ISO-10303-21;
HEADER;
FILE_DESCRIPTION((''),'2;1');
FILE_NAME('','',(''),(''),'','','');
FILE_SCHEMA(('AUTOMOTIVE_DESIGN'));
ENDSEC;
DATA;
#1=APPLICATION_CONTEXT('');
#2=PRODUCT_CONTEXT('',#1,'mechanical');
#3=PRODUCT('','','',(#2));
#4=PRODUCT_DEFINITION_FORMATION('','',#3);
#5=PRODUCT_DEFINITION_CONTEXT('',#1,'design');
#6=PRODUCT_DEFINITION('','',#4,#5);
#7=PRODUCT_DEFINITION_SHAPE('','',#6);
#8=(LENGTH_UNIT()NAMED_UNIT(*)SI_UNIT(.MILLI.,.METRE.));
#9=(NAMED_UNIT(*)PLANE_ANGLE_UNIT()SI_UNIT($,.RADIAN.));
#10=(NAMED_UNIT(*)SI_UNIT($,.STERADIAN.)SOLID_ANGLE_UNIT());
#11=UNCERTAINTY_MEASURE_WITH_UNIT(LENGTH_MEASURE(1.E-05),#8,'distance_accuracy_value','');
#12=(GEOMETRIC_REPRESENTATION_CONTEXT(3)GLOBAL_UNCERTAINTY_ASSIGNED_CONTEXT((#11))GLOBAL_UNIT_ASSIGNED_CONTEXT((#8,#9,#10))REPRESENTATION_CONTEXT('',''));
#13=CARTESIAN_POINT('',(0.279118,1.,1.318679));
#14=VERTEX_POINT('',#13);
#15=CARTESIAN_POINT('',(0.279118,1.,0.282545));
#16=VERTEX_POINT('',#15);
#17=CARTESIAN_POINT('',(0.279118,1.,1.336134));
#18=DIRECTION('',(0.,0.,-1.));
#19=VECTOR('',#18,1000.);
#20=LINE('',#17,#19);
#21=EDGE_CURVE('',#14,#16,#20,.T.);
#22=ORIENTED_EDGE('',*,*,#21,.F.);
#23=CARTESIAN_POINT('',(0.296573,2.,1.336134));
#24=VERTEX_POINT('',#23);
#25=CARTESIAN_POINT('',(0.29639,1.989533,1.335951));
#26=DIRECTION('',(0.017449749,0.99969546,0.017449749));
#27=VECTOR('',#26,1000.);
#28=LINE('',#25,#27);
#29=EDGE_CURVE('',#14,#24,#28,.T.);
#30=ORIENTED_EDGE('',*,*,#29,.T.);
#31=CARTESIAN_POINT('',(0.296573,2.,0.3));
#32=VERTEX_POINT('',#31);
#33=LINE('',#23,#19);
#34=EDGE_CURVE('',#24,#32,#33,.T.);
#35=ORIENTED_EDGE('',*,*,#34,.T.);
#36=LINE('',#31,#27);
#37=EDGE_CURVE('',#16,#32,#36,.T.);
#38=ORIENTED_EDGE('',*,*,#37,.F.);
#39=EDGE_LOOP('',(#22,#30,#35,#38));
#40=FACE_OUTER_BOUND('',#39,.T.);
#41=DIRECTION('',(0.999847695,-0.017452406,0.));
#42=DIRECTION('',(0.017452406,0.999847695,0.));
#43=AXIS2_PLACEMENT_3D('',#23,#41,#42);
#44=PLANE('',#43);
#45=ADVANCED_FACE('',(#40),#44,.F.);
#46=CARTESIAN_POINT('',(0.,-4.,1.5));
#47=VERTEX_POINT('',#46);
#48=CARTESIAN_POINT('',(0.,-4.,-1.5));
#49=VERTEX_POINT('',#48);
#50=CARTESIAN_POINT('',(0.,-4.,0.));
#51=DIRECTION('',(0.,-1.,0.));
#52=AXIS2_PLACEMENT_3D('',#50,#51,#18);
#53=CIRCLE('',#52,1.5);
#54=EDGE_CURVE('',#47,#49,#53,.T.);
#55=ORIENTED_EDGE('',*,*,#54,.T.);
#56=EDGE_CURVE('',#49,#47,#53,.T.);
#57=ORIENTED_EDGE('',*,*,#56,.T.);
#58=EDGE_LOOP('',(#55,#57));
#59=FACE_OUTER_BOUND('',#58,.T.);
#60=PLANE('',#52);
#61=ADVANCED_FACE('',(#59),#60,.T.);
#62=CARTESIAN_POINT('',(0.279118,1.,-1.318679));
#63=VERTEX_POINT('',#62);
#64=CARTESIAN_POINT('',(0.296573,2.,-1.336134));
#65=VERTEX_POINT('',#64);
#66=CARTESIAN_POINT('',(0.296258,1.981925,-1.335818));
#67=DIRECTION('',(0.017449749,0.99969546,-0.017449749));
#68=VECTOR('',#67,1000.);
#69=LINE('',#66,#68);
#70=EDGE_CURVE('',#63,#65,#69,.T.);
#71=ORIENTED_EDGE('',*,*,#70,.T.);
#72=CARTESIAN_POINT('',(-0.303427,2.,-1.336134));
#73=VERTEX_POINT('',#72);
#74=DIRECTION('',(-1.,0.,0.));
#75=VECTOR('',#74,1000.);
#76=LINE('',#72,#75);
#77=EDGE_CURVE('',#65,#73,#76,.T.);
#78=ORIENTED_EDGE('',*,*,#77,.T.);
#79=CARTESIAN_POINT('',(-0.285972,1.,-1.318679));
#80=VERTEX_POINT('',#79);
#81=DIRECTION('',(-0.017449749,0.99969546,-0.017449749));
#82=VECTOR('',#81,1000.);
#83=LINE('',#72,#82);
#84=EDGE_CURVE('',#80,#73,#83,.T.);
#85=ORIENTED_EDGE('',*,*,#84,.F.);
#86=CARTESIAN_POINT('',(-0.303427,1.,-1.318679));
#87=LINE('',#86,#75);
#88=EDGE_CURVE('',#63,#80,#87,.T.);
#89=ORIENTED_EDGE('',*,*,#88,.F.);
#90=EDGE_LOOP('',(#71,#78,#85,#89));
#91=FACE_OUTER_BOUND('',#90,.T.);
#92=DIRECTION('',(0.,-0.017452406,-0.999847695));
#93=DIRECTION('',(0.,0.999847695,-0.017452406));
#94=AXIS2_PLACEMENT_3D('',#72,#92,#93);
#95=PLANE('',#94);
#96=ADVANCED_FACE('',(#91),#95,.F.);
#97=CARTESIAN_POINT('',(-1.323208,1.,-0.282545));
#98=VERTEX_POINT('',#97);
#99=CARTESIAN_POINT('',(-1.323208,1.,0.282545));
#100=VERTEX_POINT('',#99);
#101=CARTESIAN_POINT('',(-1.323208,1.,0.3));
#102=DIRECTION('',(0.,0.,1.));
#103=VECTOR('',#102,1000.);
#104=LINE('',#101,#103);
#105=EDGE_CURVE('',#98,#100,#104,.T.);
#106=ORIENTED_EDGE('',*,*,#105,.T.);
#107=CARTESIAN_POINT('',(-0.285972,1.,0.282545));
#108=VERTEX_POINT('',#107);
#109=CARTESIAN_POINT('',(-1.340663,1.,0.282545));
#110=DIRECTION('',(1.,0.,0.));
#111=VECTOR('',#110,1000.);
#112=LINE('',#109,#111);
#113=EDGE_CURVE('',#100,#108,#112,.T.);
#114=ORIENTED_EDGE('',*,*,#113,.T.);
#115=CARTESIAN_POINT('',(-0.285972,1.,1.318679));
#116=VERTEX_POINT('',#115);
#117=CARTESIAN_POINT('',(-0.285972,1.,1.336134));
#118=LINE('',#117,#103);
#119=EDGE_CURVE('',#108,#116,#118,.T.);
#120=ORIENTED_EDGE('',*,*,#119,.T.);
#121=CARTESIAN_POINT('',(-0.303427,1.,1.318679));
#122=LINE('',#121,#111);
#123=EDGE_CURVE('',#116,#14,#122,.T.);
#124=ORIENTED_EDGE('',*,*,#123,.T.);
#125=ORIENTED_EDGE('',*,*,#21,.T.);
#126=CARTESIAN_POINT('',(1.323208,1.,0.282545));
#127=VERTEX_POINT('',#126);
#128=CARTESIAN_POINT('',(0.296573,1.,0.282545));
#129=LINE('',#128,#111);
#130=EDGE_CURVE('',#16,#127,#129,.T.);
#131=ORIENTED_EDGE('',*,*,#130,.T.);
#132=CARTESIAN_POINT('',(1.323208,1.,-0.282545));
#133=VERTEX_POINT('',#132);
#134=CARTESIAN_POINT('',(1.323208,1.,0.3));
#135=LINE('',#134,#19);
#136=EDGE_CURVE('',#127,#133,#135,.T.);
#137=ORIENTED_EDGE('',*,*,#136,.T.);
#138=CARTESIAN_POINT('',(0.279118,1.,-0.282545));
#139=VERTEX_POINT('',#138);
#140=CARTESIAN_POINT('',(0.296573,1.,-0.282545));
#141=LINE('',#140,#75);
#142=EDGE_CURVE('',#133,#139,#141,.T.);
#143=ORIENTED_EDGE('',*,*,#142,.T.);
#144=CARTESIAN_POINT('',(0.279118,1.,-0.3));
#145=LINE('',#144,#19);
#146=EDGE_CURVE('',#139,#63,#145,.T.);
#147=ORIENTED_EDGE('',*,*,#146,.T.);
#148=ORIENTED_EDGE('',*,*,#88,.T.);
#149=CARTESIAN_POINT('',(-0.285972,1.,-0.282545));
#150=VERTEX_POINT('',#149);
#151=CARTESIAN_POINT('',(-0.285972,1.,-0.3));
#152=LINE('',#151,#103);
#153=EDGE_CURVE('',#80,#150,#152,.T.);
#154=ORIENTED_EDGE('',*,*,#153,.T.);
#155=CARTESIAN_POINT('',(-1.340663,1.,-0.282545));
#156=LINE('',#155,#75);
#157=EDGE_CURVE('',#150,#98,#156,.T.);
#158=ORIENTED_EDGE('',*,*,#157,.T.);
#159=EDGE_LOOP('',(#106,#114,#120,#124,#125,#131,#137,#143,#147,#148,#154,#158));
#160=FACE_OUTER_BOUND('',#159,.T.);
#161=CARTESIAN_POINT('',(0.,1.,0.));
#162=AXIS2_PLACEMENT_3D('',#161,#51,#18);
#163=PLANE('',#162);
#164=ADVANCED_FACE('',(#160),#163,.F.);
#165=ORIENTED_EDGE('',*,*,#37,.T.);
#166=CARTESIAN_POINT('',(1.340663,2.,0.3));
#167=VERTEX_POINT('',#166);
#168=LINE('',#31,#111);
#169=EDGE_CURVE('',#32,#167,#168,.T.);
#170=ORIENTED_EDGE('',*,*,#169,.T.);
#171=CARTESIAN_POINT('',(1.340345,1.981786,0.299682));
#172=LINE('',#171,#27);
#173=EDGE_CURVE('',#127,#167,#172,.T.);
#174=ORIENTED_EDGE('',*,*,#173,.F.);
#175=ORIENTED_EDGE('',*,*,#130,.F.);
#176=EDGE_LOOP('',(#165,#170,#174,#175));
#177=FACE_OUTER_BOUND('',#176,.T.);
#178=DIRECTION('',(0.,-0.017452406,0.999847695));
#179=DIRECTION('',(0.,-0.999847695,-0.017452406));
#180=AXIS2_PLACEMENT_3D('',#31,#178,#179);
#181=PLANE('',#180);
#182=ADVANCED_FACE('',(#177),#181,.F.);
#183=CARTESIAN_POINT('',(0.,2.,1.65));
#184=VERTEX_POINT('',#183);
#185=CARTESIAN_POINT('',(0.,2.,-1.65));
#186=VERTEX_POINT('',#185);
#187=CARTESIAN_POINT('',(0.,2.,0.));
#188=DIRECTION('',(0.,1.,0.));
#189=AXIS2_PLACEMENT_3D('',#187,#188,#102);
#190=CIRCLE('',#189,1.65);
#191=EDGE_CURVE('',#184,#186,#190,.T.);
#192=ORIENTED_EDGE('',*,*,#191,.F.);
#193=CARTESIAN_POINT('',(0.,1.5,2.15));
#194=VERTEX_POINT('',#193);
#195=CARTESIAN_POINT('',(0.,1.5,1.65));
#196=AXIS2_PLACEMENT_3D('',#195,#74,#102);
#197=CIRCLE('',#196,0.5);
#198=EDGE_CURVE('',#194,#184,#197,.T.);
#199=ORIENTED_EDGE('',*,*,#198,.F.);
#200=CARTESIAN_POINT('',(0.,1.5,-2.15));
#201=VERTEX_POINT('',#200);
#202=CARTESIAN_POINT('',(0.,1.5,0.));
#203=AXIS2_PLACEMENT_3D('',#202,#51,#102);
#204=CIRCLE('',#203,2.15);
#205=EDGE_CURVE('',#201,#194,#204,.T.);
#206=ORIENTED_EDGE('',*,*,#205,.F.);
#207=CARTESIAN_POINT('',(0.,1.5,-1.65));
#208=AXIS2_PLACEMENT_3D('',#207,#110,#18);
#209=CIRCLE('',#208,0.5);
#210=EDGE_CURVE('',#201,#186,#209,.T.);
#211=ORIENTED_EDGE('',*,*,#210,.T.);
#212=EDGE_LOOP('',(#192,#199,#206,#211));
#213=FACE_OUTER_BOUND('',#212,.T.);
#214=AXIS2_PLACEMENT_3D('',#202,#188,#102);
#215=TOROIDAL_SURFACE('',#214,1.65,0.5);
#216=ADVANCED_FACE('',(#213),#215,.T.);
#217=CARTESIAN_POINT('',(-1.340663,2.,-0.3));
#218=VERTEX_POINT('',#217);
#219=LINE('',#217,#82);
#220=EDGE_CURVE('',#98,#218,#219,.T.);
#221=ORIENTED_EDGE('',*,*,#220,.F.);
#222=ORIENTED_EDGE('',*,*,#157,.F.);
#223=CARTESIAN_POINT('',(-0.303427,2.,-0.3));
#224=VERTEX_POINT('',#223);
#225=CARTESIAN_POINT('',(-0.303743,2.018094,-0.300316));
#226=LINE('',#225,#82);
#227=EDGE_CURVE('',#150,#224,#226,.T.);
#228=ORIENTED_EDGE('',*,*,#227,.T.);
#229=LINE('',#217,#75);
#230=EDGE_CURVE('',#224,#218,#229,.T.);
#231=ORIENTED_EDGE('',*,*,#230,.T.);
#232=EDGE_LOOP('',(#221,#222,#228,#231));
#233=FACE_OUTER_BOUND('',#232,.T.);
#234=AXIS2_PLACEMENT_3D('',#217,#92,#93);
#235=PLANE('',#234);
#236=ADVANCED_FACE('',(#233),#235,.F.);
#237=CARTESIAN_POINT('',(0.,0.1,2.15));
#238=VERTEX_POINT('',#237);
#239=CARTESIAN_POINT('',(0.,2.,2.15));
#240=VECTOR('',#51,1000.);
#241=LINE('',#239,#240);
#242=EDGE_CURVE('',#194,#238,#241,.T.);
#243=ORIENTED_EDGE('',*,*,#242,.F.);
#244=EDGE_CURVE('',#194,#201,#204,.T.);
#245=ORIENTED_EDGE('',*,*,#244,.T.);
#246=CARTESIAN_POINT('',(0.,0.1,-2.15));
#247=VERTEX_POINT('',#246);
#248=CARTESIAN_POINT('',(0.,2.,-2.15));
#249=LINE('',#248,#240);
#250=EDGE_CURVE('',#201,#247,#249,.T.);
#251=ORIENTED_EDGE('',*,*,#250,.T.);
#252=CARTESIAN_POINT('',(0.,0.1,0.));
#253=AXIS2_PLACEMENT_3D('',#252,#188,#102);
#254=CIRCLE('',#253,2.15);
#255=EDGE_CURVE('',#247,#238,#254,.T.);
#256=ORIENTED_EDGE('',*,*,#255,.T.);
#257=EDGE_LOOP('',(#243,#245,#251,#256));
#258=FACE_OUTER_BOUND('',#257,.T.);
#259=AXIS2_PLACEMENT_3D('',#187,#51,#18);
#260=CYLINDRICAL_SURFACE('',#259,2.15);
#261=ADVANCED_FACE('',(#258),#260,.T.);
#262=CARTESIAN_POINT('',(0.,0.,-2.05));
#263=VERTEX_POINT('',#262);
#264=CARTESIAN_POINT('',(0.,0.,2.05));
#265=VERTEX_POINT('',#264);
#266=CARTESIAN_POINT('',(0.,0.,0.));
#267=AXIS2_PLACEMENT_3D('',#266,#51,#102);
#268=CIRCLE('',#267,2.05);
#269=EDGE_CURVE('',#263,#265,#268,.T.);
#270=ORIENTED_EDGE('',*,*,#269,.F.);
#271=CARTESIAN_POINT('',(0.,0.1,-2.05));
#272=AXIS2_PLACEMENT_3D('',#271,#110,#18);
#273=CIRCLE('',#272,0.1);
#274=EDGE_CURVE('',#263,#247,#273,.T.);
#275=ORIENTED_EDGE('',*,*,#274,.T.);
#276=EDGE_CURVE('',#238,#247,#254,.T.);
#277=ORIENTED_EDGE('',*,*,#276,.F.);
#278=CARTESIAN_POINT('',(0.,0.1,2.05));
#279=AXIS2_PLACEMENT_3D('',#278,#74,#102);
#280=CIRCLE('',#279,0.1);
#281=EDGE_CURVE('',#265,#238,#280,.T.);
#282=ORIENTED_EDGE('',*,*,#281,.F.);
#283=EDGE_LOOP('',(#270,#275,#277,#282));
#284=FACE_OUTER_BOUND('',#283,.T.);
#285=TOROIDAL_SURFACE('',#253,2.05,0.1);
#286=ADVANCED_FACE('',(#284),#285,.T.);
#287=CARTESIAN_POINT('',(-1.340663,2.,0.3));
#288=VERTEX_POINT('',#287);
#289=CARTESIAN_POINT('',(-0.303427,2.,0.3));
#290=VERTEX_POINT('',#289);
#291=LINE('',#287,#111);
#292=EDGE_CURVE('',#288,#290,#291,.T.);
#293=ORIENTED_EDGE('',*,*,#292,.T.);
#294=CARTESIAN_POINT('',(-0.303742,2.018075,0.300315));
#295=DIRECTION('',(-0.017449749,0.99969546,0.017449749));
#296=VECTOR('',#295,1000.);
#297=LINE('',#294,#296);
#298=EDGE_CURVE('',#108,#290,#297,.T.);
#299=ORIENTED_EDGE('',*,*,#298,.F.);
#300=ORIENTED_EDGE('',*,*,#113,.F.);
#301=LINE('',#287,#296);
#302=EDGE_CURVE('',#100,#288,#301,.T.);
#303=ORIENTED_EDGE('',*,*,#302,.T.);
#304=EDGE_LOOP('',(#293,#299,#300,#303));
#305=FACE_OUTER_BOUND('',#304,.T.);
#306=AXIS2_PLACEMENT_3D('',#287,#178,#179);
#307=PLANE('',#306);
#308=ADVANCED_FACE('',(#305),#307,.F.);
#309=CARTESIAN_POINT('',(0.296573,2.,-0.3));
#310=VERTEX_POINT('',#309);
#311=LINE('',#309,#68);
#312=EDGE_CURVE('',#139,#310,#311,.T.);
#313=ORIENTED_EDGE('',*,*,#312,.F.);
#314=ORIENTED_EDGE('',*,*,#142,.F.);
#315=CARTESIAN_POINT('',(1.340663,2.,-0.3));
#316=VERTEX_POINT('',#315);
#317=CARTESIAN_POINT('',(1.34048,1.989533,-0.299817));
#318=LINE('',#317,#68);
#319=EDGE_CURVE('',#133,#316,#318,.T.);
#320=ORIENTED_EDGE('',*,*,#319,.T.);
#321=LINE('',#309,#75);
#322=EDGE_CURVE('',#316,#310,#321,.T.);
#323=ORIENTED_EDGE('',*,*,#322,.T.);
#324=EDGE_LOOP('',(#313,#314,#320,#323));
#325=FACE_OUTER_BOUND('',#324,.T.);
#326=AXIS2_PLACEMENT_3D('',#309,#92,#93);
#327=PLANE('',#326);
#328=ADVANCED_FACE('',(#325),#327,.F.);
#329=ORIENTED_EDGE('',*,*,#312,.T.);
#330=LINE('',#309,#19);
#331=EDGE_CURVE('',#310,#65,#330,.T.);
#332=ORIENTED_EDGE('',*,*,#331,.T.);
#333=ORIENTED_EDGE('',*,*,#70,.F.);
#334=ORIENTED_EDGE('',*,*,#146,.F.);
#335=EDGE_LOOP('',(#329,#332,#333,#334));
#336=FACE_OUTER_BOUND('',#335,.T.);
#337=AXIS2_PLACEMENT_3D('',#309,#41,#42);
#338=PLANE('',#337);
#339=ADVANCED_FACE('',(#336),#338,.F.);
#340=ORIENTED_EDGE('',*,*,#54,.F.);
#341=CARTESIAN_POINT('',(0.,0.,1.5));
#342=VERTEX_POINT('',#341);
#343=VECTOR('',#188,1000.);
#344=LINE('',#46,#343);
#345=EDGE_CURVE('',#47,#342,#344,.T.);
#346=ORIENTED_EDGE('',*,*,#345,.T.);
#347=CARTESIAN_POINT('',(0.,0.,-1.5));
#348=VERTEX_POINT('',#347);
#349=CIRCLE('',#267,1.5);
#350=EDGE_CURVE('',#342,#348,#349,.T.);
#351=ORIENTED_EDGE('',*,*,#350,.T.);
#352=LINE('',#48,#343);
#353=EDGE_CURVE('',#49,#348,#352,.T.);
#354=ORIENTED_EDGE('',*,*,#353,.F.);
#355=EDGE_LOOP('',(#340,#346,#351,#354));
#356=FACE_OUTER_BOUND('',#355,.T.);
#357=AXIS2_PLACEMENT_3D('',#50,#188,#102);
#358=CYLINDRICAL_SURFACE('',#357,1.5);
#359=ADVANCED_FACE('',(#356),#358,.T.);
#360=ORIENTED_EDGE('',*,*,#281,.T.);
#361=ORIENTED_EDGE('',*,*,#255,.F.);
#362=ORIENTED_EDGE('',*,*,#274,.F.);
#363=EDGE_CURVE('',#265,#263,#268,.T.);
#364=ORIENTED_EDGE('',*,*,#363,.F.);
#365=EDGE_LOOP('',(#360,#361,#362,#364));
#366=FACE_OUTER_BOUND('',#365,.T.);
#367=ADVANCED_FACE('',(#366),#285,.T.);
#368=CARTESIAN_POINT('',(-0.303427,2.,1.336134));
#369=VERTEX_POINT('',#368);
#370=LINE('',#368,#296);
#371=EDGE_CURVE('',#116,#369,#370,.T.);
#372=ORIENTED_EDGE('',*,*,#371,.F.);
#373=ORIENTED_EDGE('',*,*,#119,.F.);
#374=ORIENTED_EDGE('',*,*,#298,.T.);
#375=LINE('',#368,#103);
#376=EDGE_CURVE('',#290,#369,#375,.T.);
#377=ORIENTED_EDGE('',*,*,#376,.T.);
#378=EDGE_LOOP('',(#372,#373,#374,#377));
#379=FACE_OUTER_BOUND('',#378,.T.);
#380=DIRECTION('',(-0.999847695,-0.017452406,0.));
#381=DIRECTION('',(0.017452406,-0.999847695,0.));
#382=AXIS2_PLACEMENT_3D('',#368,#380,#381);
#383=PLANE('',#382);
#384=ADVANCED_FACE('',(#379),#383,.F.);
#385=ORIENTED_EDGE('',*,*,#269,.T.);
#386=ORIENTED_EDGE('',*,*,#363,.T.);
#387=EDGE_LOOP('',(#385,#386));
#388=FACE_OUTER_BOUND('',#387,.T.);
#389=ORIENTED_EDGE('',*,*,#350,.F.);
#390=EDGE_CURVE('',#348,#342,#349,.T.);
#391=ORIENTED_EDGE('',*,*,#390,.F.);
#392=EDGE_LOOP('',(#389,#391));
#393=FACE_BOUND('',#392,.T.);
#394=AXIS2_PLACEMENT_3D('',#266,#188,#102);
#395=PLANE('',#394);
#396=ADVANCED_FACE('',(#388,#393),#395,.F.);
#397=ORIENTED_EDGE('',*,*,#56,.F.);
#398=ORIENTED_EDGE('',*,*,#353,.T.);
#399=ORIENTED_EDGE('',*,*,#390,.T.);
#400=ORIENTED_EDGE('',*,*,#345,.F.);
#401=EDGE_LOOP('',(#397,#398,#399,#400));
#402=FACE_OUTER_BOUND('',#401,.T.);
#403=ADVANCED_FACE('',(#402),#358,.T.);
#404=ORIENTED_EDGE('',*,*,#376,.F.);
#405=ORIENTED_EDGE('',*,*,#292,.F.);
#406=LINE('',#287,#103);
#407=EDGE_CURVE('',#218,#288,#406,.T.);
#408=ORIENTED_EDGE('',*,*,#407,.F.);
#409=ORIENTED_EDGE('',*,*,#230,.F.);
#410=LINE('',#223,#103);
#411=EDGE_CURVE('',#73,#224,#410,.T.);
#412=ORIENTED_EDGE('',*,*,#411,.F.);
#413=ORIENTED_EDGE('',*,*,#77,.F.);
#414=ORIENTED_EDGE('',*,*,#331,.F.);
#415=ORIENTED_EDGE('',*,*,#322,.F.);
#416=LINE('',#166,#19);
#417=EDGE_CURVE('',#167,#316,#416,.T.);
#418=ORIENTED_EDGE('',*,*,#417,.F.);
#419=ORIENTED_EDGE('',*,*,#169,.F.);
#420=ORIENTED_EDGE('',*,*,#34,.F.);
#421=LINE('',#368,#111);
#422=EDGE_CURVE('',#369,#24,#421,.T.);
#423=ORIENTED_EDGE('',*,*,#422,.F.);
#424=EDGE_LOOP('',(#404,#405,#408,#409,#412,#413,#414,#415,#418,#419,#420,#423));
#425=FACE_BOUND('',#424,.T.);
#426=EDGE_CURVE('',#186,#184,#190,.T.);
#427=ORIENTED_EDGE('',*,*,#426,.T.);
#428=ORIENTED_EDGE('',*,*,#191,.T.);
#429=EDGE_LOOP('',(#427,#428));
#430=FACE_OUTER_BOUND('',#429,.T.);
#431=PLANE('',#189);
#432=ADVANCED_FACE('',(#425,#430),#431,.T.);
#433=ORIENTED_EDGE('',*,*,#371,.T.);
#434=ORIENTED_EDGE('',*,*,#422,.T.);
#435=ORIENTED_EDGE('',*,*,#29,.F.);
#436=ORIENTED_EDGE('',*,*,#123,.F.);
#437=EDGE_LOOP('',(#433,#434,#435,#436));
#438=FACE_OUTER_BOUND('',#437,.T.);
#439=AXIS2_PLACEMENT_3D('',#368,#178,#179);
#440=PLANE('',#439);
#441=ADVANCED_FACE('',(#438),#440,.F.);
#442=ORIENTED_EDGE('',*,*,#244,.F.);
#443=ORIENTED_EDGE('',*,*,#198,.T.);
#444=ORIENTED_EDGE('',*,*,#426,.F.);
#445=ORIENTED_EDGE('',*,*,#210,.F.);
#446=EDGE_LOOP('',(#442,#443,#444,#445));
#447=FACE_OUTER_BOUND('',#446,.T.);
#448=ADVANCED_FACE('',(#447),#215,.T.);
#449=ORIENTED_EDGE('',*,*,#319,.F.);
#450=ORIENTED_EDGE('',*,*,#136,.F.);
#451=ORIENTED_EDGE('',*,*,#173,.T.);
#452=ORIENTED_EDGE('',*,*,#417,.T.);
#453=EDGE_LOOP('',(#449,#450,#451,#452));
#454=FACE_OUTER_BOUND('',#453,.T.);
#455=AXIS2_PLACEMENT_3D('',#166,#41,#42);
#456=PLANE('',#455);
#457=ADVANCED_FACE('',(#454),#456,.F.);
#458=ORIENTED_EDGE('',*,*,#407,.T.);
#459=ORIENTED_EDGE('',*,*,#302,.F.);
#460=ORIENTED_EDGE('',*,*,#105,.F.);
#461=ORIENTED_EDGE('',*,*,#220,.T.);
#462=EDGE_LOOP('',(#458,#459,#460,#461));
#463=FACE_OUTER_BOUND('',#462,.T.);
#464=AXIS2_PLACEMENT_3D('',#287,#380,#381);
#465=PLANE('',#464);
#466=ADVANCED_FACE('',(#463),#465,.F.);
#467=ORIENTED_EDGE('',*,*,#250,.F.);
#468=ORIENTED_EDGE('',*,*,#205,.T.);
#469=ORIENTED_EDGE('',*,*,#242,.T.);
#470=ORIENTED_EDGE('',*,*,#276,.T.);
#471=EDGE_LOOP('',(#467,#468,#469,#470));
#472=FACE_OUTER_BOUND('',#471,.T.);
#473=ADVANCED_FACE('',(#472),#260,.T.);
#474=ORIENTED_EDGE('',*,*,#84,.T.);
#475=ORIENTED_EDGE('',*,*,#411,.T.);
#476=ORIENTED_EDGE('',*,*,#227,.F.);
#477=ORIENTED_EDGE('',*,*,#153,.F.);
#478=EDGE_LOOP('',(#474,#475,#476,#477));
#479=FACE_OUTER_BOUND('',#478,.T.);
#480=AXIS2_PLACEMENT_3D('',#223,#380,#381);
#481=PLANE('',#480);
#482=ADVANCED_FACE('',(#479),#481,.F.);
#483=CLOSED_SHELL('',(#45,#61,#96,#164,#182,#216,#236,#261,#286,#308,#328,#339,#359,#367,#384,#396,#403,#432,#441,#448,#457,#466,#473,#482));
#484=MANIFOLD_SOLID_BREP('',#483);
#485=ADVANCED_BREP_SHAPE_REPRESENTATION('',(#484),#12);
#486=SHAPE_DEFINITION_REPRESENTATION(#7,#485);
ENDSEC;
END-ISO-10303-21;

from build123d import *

# Parameters (mm, degrees)
SKETCH1_R           = 2.15
BOSS_EXTRUDE1_DEPTH = 2
SKETCH2_R           = 1.5
BOSS_EXTRUDE2_DEPTH = 4
FILLET1_R           = 0.5
FILLET2_R           = 0.1
CUT_EXTRUDE1_DEPTH  = 1
CUT_EXTRUDE1_DRAFT  = -1


with BuildPart() as part:
    # Sketch1 → Boss-Extrude1 (new body)
    with BuildSketch(Plane(origin=(0, 0, 0), x_dir=(1, 0, 0), z_dir=(0, 1, 0))):
        with Locations(Location((0, 0, 0), (0, 0, 270))):
            Circle(SKETCH1_R)
    extrude(amount=BOSS_EXTRUDE1_DEPTH)

    # Sketch2 → Boss-Extrude2 (add)
    with BuildSketch(Plane.XZ):
        with Locations(Location((0, 0, 0), (0, 0, 90))):
            Circle(SKETCH2_R)
    extrude(amount=BOSS_EXTRUDE2_DEPTH)

    # Fillet1
    fillet1_edges = [part.edges().sort_by_distance(p)[0] for p in [
        (0, 2, -2.15),
    ]]
    fillet(fillet1_edges, radius=FILLET1_R)

    # Fillet2
    fillet2_edges = [part.edges().sort_by_distance(p)[0] for p in [
        (0, 0, -2.15),
    ]]
    fillet(fillet2_edges, radius=FILLET2_R)


with BuildPart() as cut_extrude1_tool:
    # Sketch3 → Cut-Extrude1 (with draft: the straight prism first)
    with BuildSketch(Plane(origin=(0, 2, 0), x_dir=(1, 0, 0), z_dir=(0, 1, 0))):
        Polygon((0.296573117, 0.3), (0.296573117, 1.336133674), (-0.303426883, 1.336133674), (-0.303426883, 0.3), (-1.340662941, 0.3), (-1.340662941, -0.3), (-0.303426883, -0.3), (-0.303426883, -1.336133674), (0.296573117, -1.336133674), (0.296573117, -0.3), (1.340662941, -0.3), (1.340662941, 0.3), align=None)
    extrude(amount=-CUT_EXTRUDE1_DEPTH)
    # Cut-Extrude1: the draft: its side faces are tilted about the plane it starts from
    cut_extrude1_sides = [cut_extrude1_tool.faces().sort_by_distance(p)[0] for p in [
        (0.296573117, 1.5, -0.818066837),
        (-0.003426883, 1.5, -1.336133674),
        (-0.303426883, 1.5, -0.818066837),
        (-0.822044912, 1.5, -0.3),
        (-1.340662941, 1.5, 0),
        (-0.822044912, 1.5, 0.3),
        (-0.303426883, 1.5, 0.818066837),
        (-0.003426883, 1.5, 1.336133674),
        (0.296573117, 1.5, 0.818066837),
        (0.818618029, 1.5, 0.3),
        (1.340662941, 1.5, 0),
        (0.818618029, 1.5, -0.3),
    ]]
    draft(cut_extrude1_sides, Plane(origin=(0, 2, 0), x_dir=(1, 0, 0), z_dir=(0, 1, 0)), CUT_EXTRUDE1_DRAFT)


with BuildPart() as part_1:
    add(part.part)

    # Cut-Extrude1: cut by cut_extrude1_tool
    add(cut_extrude1_tool.part, mode=Mode.SUBTRACT)


solid = part_1.part
